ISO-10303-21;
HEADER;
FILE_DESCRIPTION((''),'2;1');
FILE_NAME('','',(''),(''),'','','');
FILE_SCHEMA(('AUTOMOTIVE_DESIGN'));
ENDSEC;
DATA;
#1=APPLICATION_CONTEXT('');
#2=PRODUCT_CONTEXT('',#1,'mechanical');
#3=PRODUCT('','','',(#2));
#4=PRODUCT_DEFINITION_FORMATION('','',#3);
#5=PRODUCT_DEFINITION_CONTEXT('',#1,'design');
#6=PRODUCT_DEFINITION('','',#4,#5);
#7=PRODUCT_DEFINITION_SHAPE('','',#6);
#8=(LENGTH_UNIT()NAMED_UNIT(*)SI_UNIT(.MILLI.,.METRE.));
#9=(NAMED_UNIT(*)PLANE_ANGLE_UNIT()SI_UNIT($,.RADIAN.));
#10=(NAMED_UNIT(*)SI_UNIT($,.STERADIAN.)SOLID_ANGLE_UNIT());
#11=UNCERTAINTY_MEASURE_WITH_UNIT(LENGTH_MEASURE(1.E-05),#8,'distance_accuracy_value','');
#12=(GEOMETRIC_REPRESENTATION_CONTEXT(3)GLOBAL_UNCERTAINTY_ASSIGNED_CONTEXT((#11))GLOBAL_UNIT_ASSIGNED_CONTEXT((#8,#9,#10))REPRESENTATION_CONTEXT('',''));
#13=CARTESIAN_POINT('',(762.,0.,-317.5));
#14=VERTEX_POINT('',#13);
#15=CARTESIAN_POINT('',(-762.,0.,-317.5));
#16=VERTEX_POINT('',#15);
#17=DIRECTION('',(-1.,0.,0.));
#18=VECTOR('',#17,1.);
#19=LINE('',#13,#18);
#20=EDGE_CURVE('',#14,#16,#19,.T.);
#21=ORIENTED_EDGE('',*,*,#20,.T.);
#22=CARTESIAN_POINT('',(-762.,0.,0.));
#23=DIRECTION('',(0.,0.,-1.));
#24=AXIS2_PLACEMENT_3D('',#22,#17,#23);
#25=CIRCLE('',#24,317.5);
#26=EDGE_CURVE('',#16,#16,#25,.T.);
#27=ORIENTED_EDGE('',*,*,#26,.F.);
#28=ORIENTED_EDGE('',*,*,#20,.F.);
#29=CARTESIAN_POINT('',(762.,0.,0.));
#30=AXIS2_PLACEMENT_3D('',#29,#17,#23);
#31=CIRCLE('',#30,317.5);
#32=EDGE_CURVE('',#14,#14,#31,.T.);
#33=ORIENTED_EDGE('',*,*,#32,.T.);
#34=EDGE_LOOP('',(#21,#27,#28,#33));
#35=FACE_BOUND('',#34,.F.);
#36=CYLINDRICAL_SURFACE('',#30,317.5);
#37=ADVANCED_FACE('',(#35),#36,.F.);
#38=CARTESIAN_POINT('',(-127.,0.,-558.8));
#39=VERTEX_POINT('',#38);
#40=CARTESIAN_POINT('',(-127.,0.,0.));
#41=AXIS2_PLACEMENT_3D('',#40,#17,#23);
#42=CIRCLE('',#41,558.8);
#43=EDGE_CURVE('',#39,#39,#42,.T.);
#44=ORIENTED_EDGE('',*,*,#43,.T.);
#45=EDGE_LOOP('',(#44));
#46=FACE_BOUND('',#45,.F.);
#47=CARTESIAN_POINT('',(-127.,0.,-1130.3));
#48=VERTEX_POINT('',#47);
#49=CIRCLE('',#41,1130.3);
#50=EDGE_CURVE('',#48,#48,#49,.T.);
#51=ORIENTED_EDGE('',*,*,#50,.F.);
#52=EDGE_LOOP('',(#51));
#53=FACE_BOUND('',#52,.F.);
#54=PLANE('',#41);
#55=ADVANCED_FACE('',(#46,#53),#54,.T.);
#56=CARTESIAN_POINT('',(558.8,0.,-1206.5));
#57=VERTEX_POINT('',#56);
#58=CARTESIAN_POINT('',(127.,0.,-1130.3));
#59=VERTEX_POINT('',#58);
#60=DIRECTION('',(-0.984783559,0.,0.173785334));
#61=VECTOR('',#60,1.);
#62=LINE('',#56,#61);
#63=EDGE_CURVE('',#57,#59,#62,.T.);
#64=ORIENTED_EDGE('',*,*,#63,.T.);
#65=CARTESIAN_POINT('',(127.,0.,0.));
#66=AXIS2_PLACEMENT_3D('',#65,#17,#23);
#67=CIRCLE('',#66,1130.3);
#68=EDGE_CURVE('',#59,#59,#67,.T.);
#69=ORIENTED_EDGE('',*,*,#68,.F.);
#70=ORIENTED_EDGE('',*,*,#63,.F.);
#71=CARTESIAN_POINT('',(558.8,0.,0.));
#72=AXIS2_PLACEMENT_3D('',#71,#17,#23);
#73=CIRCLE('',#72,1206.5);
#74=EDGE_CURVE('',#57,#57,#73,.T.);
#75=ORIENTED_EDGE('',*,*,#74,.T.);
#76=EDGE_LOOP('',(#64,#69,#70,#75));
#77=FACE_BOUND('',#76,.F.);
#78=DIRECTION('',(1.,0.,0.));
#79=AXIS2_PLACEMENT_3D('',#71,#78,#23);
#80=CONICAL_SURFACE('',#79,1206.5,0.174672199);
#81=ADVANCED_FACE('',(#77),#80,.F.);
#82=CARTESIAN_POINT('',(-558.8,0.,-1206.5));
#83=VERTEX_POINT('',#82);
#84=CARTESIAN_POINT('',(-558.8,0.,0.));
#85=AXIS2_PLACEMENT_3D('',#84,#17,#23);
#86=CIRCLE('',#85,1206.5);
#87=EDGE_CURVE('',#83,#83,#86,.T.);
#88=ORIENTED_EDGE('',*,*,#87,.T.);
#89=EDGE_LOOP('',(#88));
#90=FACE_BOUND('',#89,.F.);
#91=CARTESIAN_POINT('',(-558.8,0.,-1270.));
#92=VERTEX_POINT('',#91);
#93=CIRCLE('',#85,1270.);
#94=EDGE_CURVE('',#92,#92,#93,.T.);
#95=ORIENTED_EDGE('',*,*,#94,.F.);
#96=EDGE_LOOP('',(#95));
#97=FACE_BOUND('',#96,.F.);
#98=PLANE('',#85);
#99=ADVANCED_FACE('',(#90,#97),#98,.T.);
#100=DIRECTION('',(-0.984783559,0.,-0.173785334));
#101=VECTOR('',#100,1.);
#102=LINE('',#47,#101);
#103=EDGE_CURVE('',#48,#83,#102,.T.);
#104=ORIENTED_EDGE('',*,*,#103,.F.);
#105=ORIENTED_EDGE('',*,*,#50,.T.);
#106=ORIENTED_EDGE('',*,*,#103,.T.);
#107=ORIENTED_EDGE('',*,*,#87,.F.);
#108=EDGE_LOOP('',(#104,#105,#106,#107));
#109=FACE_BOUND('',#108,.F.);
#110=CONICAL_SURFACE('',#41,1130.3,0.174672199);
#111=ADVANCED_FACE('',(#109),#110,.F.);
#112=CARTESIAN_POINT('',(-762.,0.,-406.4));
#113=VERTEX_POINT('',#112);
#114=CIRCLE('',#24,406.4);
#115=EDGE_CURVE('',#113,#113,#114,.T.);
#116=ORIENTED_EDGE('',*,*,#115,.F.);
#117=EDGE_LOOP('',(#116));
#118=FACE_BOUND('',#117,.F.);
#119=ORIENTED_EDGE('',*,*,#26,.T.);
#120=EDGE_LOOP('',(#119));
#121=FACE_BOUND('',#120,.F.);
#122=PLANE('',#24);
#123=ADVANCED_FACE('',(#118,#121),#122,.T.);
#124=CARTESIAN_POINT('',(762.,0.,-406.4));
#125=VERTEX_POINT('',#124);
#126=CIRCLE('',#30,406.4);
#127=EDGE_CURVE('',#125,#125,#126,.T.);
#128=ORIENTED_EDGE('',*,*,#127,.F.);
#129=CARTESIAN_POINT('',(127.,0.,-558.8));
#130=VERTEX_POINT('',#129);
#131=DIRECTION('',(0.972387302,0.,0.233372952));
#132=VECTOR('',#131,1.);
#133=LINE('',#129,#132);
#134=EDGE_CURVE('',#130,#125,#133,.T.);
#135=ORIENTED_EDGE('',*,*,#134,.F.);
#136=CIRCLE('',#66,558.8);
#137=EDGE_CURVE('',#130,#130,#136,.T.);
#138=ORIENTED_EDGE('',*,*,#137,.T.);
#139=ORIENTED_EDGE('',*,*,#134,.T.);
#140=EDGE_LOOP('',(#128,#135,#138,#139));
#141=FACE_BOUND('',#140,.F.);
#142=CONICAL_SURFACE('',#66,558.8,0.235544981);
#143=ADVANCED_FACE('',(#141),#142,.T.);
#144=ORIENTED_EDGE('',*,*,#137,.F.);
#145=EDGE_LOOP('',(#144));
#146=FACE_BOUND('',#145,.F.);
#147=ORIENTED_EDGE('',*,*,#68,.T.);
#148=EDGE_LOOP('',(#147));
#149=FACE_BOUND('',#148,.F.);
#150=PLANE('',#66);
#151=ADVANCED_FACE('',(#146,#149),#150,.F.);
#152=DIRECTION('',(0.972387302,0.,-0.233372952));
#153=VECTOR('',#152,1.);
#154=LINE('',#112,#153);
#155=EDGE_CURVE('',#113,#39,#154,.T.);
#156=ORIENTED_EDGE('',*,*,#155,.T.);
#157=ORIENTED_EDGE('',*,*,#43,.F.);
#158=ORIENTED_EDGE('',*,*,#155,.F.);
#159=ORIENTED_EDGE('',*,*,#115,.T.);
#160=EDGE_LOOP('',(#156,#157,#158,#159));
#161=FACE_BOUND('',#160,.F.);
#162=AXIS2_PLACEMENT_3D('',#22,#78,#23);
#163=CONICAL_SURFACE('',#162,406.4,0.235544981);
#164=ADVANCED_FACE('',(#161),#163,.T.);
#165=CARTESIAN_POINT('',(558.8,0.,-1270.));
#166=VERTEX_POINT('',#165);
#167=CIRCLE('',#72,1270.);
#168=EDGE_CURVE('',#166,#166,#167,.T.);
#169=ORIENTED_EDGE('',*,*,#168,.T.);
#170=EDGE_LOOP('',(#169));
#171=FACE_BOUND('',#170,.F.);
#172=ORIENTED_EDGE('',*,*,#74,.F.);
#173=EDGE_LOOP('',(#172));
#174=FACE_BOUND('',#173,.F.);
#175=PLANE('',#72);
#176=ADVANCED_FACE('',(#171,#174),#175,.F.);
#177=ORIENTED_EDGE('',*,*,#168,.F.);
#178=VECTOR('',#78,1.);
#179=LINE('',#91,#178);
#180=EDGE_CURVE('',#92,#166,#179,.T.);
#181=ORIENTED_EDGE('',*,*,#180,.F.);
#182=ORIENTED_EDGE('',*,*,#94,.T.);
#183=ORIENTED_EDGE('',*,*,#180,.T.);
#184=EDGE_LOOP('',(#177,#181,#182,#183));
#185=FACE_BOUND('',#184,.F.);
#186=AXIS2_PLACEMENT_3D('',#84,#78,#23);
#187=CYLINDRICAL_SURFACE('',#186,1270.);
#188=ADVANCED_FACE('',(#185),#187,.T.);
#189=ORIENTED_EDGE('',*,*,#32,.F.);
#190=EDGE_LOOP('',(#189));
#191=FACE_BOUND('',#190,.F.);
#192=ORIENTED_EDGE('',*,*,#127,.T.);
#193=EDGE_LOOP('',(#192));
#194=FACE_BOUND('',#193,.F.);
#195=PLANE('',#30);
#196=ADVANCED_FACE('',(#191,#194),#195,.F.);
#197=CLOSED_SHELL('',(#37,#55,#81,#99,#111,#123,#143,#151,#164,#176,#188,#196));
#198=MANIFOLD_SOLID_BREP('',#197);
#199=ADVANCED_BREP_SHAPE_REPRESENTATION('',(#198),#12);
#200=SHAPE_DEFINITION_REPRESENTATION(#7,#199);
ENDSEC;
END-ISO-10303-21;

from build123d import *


with BuildPart() as part:
    # Sketch1 → Revolve1 (revolve)
    with BuildSketch(Plane.XY, mode=Mode.PRIVATE) as revolve1_sk:
        Polygon((-762, 317.5), (-762, 406.4), (-127, 558.8), (-127, 1130.3), (-558.8, 1206.5), (-558.8, 1270), (558.8, 1270), (558.8, 1206.5), (127, 1130.3), (127, 558.8), (762, 406.4), (762, 317.5), align=None)
    revolve(revolve1_sk.sketch.rotate(Axis((0, 0, 0), (-1, 0, 0)), 90), axis=Axis((0, 0, 0), (-1, 0, 0)))


solid = part.part
